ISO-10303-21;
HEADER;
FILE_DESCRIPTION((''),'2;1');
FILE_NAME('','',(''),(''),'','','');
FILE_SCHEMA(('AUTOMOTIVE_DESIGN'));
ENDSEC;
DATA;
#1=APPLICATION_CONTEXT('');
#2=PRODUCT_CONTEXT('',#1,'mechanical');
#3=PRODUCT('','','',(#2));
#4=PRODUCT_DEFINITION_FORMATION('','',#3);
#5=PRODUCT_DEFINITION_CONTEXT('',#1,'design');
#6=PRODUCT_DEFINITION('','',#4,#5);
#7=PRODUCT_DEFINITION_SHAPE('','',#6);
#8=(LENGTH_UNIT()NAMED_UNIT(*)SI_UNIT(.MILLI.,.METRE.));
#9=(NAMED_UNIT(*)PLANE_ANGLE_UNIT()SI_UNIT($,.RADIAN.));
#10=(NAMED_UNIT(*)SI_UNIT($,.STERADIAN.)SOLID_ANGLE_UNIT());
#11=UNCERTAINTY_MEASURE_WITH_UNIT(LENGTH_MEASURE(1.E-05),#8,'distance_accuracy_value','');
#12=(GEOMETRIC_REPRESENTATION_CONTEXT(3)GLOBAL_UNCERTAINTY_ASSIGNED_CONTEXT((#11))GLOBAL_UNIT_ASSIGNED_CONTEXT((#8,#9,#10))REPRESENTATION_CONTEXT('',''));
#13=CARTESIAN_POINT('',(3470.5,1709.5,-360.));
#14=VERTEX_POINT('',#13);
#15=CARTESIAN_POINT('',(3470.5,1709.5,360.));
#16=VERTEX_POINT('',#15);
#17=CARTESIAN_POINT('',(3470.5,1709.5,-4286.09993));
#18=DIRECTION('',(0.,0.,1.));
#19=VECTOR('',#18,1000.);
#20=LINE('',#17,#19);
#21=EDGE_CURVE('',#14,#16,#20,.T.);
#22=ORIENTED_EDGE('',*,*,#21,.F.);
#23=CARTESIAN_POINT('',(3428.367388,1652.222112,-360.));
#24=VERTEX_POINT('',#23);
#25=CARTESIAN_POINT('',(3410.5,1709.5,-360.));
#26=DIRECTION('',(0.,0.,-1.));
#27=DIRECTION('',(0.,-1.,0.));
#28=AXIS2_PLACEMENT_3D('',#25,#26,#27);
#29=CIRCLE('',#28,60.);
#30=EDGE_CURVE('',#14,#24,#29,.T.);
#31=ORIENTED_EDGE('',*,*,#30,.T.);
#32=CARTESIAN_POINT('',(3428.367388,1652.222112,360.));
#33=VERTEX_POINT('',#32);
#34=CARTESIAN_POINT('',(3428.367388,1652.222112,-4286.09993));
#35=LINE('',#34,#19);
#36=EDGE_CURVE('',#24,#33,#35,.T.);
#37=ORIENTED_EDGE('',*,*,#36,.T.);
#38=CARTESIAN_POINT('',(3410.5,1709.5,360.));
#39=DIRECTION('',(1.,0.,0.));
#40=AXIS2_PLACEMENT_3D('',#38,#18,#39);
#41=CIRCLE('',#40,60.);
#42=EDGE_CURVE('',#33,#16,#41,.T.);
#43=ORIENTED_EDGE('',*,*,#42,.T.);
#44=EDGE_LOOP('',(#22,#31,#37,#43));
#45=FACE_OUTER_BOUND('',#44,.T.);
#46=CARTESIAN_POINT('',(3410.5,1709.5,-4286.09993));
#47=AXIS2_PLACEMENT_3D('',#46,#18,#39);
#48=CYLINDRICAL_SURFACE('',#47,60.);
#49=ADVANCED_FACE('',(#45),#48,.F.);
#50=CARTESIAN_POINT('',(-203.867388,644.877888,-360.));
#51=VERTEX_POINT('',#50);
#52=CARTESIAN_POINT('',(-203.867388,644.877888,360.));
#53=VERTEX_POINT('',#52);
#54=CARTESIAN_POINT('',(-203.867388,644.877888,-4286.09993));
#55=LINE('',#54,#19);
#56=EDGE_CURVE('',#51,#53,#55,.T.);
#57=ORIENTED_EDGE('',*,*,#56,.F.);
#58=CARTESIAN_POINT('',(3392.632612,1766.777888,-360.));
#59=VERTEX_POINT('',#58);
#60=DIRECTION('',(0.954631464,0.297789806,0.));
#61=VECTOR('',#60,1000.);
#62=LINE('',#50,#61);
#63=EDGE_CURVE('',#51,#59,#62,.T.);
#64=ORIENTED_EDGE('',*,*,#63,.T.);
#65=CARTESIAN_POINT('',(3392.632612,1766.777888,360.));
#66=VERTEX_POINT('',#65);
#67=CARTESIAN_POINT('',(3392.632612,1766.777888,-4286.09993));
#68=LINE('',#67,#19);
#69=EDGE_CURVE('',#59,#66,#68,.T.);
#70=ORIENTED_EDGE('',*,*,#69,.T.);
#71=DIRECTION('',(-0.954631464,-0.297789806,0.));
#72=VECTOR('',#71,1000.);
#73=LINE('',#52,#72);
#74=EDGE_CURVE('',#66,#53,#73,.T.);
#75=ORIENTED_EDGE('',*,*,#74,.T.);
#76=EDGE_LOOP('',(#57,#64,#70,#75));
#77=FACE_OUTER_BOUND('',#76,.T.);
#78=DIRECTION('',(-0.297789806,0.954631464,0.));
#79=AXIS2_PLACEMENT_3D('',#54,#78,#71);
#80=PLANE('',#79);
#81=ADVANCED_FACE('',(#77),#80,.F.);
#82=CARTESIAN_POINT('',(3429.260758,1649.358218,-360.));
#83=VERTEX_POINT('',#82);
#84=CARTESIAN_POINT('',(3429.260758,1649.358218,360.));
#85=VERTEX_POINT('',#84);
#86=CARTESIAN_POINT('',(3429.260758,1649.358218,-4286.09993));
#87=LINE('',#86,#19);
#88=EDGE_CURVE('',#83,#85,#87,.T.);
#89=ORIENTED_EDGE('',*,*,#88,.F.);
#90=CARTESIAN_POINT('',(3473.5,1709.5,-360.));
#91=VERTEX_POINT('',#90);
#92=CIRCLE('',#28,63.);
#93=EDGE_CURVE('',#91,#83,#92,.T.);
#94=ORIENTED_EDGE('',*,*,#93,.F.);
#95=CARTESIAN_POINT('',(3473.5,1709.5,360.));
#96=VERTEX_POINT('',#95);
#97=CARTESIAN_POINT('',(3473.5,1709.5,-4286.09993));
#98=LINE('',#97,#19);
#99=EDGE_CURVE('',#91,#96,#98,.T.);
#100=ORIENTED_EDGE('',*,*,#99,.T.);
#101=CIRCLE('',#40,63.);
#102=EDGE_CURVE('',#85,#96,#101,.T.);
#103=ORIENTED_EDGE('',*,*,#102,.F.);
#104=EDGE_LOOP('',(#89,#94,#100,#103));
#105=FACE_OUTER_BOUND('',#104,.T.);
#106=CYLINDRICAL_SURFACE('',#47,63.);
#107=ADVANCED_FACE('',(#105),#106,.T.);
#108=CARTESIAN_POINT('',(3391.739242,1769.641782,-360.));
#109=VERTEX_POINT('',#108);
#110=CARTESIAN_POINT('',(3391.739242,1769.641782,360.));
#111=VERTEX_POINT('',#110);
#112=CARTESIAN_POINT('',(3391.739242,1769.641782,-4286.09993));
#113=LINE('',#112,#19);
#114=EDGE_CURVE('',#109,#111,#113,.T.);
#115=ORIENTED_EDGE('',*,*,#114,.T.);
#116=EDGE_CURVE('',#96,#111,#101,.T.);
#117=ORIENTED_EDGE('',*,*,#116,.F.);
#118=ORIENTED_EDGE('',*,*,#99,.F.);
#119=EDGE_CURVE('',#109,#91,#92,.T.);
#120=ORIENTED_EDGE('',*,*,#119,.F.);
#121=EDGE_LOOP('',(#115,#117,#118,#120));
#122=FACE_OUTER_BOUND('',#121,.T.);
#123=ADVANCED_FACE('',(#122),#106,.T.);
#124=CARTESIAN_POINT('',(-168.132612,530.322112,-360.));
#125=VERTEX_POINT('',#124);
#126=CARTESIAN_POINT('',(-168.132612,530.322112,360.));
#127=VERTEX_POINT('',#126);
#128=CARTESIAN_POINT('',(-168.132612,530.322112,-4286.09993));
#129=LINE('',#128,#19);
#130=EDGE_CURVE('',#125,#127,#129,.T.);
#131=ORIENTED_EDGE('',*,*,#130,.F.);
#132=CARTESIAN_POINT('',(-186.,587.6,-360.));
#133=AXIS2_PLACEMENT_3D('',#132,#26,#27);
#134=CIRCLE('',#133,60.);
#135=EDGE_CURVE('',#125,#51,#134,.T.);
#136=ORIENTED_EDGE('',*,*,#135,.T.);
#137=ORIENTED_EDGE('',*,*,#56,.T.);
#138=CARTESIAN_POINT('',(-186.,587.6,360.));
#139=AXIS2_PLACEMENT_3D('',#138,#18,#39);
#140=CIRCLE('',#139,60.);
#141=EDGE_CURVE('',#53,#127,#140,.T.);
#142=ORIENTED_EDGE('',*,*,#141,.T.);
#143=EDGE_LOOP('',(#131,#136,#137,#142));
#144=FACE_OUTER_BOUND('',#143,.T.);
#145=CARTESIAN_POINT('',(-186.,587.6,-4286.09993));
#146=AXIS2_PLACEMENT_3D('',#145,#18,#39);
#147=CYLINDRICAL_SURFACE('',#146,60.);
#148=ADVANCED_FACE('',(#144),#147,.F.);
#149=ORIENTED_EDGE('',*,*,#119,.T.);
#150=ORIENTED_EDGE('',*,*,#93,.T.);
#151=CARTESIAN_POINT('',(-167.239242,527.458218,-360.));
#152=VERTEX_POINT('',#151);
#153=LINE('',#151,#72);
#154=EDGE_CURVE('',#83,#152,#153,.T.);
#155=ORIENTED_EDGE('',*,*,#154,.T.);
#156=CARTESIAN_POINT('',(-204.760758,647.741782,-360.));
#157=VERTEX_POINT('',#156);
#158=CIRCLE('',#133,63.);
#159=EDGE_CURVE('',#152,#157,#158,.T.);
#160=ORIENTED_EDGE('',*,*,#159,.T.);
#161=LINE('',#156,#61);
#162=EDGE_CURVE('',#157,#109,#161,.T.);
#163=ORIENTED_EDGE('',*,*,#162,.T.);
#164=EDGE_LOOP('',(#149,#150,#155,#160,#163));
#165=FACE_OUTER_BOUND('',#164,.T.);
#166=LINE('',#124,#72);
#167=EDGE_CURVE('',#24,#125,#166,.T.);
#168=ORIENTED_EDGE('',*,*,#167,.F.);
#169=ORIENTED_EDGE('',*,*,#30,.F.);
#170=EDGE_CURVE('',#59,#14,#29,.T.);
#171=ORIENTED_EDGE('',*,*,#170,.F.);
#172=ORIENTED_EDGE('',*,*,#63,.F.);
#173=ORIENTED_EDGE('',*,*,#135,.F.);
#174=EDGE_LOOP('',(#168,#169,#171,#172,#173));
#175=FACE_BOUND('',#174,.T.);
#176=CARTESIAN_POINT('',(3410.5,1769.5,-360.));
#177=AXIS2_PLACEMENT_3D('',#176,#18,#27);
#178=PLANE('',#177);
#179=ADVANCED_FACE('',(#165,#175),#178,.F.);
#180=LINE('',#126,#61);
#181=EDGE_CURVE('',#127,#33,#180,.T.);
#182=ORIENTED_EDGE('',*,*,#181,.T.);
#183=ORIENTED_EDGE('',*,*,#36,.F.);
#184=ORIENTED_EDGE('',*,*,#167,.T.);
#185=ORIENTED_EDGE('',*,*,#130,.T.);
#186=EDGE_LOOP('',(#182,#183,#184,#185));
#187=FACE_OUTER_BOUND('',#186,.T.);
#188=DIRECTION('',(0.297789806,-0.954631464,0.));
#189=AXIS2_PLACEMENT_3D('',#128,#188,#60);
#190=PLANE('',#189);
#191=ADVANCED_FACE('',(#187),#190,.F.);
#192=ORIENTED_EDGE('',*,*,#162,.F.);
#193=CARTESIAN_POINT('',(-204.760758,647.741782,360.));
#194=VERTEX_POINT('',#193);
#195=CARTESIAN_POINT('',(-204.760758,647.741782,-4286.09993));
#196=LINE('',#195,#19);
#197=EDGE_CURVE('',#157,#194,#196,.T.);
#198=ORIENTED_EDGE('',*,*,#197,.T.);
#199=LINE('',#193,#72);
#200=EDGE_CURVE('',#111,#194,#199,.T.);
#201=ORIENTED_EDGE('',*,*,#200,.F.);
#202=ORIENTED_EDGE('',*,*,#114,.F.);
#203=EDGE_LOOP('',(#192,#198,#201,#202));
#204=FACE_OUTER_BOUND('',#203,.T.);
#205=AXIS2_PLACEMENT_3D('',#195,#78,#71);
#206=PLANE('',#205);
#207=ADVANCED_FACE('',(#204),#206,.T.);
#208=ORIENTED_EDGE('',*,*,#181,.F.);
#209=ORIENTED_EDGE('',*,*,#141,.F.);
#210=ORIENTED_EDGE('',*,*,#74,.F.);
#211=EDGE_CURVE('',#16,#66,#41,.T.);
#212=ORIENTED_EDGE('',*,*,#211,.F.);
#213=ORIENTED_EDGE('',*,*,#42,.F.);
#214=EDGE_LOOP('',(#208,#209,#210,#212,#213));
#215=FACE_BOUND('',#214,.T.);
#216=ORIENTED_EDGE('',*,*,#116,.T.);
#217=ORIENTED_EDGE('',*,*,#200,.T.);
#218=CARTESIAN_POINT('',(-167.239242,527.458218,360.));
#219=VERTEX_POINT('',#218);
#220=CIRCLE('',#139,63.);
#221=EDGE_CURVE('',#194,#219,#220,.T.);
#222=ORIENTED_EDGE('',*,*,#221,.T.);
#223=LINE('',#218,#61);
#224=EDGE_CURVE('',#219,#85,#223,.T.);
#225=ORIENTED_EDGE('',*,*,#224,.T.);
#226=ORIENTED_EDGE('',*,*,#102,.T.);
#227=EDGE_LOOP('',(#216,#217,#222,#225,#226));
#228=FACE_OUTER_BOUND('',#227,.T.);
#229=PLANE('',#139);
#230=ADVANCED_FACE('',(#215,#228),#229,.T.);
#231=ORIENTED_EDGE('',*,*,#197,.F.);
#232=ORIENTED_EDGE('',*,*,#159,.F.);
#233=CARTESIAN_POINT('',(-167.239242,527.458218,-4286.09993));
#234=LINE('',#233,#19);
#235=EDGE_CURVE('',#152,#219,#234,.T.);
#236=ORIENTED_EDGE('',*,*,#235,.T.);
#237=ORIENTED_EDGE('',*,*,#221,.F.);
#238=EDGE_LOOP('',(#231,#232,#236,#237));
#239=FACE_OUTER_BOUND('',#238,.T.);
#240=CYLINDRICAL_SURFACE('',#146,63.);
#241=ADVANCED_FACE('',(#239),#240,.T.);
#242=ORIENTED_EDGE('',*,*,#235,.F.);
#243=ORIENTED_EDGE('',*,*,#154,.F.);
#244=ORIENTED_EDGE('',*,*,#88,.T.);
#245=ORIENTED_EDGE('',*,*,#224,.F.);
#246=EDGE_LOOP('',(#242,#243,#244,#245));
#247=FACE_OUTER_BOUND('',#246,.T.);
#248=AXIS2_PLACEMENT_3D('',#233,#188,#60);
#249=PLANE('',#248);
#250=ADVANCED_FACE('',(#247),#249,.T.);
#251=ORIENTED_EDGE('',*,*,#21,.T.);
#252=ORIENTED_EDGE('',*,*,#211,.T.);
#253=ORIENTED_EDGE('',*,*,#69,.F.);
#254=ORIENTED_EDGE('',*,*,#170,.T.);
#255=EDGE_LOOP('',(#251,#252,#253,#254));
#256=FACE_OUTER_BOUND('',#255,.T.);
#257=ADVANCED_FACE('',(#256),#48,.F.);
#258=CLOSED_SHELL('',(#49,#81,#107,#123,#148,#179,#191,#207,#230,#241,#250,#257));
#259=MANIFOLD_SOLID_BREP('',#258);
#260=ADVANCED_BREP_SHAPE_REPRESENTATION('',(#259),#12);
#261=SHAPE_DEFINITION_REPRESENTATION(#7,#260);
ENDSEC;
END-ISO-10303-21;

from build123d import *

# Parameters (mm, degrees)
EXTRUDE_1_DEPTH = 720


with BuildPart() as part:
    # 草图1 → 凸台-拉伸1 (new body)
    with BuildSketch(Plane.XY.offset(360)):
        with BuildLine():
            Line((-204.760757807, 647.741782203), (3391.739242193, 1769.641782203))
            ThreePointArc((3391.739242193, 1769.641782203), (3470.641782203, 1728.260757807), (3429.260757807, 1649.358217797))
            Line((3429.260757807, 1649.358217797), (-167.239242193, 527.458217797))
            ThreePointArc((-167.239242193, 527.458217797), (-246.141782203, 568.839242193), (-204.760757807, 647.741782203))
        make_face()
        with BuildLine():
            Line((-203.867388388, 644.877887812), (3392.632611612, 1766.777887812))
            ThreePointArc((3392.632611612, 1766.777887812), (3467.777887812, 1727.367388388), (3428.367388388, 1652.222112188))
            Line((3428.367388388, 1652.222112188), (-168.132611612, 530.322112188))
            ThreePointArc((-168.132611612, 530.322112188), (-243.277887812, 569.732611612), (-203.867388388, 644.877887812))
        make_face(mode=Mode.SUBTRACT)
    extrude(amount=-EXTRUDE_1_DEPTH)


solid = part.part
